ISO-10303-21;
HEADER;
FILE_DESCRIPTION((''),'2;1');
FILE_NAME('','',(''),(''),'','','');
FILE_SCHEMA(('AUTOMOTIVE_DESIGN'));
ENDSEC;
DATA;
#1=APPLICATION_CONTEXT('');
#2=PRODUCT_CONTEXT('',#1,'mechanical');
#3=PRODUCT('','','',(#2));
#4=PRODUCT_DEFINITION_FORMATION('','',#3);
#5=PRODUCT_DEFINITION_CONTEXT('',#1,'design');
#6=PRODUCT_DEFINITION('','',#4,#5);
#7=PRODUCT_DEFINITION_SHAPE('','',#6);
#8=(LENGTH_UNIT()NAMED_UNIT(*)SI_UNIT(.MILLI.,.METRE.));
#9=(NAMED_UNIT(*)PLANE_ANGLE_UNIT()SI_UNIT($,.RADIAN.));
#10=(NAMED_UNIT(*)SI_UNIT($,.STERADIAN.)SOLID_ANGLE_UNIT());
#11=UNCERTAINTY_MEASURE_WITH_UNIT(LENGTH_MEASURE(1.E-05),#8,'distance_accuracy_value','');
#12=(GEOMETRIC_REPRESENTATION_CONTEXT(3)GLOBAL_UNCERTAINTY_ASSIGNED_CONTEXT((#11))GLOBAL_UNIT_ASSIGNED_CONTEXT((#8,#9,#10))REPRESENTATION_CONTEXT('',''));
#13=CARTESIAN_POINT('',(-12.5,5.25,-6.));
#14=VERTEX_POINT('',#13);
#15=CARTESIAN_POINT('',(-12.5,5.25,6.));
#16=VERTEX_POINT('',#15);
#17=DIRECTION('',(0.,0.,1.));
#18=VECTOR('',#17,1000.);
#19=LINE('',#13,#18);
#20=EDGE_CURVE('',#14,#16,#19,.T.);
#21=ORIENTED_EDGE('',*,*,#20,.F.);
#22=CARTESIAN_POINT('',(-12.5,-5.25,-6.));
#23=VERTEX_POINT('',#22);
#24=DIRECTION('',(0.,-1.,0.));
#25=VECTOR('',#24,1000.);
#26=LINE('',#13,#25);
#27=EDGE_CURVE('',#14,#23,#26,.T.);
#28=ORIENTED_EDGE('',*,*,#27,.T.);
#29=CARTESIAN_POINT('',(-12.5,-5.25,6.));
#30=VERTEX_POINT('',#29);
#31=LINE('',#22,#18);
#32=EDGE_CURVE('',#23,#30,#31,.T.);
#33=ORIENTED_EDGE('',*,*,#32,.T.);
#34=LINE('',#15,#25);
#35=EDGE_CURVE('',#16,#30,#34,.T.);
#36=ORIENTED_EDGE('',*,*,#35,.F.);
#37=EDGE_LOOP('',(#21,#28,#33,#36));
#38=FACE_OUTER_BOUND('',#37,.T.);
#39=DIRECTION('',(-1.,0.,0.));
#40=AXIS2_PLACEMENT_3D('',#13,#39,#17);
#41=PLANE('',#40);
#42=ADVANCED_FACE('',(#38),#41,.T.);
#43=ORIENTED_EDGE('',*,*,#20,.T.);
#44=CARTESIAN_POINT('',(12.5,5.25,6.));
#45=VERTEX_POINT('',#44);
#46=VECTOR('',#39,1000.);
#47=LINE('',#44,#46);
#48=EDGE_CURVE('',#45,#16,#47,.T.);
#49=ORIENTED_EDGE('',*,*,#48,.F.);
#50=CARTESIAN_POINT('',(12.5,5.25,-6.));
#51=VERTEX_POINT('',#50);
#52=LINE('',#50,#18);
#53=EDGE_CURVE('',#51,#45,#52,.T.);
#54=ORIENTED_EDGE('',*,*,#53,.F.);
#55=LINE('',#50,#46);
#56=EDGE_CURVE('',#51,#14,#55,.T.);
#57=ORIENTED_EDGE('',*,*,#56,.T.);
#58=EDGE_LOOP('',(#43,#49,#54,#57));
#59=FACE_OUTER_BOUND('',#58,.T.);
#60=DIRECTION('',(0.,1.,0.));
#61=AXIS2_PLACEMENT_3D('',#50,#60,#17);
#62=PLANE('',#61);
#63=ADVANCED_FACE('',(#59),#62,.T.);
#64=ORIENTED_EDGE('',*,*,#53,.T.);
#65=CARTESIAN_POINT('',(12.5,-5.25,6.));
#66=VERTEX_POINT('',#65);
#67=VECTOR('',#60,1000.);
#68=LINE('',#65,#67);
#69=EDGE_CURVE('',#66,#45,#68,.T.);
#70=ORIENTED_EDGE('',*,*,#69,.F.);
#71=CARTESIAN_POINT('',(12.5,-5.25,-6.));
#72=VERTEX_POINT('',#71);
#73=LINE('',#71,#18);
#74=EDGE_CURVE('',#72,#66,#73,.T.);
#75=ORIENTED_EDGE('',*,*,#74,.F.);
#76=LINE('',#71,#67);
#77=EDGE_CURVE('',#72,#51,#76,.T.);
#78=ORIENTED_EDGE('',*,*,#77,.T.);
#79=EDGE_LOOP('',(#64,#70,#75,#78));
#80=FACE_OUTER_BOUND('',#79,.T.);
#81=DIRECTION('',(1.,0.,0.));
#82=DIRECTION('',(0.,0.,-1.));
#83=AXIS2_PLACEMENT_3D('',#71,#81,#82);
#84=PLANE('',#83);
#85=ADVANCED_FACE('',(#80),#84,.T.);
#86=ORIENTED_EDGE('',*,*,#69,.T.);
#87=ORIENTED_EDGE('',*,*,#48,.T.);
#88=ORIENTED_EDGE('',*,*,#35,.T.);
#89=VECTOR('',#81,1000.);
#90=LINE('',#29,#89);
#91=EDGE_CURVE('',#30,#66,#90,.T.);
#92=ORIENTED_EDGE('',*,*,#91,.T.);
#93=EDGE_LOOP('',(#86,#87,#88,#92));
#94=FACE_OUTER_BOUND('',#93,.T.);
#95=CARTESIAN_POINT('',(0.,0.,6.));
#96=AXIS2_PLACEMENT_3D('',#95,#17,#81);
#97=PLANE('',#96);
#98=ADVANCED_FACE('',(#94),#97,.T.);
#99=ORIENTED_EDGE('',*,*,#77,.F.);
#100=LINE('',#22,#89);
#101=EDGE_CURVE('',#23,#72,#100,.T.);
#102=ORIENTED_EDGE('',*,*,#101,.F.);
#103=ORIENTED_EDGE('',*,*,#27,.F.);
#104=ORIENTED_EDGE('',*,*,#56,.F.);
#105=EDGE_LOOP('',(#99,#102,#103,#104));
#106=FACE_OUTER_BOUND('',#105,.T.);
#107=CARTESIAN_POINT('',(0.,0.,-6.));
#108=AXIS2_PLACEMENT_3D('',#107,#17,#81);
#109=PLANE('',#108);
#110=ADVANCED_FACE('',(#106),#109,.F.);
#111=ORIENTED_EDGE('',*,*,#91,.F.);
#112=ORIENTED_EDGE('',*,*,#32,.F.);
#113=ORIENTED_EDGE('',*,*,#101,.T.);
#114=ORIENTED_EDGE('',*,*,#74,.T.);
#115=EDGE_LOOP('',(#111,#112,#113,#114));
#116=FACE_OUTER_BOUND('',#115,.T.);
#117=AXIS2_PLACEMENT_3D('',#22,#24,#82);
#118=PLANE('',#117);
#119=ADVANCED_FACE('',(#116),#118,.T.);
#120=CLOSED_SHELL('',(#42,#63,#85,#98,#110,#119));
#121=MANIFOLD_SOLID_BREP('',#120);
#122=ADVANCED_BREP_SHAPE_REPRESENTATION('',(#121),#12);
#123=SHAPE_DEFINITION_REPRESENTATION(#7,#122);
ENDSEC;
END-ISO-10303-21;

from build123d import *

# Parameters (mm, degrees)
SKETCH_1_W      = 25
SKETCH_1_H      = 10.5
EXTRUDE_1_DEPTH = 6


with BuildPart() as part:
    # 草图1 → 凸台-拉伸1 (new, symmetric)
    with BuildSketch(Plane.XY):
        Rectangle(SKETCH_1_W, SKETCH_1_H)
    extrude(amount=EXTRUDE_1_DEPTH, both=True)


solid = part.part
